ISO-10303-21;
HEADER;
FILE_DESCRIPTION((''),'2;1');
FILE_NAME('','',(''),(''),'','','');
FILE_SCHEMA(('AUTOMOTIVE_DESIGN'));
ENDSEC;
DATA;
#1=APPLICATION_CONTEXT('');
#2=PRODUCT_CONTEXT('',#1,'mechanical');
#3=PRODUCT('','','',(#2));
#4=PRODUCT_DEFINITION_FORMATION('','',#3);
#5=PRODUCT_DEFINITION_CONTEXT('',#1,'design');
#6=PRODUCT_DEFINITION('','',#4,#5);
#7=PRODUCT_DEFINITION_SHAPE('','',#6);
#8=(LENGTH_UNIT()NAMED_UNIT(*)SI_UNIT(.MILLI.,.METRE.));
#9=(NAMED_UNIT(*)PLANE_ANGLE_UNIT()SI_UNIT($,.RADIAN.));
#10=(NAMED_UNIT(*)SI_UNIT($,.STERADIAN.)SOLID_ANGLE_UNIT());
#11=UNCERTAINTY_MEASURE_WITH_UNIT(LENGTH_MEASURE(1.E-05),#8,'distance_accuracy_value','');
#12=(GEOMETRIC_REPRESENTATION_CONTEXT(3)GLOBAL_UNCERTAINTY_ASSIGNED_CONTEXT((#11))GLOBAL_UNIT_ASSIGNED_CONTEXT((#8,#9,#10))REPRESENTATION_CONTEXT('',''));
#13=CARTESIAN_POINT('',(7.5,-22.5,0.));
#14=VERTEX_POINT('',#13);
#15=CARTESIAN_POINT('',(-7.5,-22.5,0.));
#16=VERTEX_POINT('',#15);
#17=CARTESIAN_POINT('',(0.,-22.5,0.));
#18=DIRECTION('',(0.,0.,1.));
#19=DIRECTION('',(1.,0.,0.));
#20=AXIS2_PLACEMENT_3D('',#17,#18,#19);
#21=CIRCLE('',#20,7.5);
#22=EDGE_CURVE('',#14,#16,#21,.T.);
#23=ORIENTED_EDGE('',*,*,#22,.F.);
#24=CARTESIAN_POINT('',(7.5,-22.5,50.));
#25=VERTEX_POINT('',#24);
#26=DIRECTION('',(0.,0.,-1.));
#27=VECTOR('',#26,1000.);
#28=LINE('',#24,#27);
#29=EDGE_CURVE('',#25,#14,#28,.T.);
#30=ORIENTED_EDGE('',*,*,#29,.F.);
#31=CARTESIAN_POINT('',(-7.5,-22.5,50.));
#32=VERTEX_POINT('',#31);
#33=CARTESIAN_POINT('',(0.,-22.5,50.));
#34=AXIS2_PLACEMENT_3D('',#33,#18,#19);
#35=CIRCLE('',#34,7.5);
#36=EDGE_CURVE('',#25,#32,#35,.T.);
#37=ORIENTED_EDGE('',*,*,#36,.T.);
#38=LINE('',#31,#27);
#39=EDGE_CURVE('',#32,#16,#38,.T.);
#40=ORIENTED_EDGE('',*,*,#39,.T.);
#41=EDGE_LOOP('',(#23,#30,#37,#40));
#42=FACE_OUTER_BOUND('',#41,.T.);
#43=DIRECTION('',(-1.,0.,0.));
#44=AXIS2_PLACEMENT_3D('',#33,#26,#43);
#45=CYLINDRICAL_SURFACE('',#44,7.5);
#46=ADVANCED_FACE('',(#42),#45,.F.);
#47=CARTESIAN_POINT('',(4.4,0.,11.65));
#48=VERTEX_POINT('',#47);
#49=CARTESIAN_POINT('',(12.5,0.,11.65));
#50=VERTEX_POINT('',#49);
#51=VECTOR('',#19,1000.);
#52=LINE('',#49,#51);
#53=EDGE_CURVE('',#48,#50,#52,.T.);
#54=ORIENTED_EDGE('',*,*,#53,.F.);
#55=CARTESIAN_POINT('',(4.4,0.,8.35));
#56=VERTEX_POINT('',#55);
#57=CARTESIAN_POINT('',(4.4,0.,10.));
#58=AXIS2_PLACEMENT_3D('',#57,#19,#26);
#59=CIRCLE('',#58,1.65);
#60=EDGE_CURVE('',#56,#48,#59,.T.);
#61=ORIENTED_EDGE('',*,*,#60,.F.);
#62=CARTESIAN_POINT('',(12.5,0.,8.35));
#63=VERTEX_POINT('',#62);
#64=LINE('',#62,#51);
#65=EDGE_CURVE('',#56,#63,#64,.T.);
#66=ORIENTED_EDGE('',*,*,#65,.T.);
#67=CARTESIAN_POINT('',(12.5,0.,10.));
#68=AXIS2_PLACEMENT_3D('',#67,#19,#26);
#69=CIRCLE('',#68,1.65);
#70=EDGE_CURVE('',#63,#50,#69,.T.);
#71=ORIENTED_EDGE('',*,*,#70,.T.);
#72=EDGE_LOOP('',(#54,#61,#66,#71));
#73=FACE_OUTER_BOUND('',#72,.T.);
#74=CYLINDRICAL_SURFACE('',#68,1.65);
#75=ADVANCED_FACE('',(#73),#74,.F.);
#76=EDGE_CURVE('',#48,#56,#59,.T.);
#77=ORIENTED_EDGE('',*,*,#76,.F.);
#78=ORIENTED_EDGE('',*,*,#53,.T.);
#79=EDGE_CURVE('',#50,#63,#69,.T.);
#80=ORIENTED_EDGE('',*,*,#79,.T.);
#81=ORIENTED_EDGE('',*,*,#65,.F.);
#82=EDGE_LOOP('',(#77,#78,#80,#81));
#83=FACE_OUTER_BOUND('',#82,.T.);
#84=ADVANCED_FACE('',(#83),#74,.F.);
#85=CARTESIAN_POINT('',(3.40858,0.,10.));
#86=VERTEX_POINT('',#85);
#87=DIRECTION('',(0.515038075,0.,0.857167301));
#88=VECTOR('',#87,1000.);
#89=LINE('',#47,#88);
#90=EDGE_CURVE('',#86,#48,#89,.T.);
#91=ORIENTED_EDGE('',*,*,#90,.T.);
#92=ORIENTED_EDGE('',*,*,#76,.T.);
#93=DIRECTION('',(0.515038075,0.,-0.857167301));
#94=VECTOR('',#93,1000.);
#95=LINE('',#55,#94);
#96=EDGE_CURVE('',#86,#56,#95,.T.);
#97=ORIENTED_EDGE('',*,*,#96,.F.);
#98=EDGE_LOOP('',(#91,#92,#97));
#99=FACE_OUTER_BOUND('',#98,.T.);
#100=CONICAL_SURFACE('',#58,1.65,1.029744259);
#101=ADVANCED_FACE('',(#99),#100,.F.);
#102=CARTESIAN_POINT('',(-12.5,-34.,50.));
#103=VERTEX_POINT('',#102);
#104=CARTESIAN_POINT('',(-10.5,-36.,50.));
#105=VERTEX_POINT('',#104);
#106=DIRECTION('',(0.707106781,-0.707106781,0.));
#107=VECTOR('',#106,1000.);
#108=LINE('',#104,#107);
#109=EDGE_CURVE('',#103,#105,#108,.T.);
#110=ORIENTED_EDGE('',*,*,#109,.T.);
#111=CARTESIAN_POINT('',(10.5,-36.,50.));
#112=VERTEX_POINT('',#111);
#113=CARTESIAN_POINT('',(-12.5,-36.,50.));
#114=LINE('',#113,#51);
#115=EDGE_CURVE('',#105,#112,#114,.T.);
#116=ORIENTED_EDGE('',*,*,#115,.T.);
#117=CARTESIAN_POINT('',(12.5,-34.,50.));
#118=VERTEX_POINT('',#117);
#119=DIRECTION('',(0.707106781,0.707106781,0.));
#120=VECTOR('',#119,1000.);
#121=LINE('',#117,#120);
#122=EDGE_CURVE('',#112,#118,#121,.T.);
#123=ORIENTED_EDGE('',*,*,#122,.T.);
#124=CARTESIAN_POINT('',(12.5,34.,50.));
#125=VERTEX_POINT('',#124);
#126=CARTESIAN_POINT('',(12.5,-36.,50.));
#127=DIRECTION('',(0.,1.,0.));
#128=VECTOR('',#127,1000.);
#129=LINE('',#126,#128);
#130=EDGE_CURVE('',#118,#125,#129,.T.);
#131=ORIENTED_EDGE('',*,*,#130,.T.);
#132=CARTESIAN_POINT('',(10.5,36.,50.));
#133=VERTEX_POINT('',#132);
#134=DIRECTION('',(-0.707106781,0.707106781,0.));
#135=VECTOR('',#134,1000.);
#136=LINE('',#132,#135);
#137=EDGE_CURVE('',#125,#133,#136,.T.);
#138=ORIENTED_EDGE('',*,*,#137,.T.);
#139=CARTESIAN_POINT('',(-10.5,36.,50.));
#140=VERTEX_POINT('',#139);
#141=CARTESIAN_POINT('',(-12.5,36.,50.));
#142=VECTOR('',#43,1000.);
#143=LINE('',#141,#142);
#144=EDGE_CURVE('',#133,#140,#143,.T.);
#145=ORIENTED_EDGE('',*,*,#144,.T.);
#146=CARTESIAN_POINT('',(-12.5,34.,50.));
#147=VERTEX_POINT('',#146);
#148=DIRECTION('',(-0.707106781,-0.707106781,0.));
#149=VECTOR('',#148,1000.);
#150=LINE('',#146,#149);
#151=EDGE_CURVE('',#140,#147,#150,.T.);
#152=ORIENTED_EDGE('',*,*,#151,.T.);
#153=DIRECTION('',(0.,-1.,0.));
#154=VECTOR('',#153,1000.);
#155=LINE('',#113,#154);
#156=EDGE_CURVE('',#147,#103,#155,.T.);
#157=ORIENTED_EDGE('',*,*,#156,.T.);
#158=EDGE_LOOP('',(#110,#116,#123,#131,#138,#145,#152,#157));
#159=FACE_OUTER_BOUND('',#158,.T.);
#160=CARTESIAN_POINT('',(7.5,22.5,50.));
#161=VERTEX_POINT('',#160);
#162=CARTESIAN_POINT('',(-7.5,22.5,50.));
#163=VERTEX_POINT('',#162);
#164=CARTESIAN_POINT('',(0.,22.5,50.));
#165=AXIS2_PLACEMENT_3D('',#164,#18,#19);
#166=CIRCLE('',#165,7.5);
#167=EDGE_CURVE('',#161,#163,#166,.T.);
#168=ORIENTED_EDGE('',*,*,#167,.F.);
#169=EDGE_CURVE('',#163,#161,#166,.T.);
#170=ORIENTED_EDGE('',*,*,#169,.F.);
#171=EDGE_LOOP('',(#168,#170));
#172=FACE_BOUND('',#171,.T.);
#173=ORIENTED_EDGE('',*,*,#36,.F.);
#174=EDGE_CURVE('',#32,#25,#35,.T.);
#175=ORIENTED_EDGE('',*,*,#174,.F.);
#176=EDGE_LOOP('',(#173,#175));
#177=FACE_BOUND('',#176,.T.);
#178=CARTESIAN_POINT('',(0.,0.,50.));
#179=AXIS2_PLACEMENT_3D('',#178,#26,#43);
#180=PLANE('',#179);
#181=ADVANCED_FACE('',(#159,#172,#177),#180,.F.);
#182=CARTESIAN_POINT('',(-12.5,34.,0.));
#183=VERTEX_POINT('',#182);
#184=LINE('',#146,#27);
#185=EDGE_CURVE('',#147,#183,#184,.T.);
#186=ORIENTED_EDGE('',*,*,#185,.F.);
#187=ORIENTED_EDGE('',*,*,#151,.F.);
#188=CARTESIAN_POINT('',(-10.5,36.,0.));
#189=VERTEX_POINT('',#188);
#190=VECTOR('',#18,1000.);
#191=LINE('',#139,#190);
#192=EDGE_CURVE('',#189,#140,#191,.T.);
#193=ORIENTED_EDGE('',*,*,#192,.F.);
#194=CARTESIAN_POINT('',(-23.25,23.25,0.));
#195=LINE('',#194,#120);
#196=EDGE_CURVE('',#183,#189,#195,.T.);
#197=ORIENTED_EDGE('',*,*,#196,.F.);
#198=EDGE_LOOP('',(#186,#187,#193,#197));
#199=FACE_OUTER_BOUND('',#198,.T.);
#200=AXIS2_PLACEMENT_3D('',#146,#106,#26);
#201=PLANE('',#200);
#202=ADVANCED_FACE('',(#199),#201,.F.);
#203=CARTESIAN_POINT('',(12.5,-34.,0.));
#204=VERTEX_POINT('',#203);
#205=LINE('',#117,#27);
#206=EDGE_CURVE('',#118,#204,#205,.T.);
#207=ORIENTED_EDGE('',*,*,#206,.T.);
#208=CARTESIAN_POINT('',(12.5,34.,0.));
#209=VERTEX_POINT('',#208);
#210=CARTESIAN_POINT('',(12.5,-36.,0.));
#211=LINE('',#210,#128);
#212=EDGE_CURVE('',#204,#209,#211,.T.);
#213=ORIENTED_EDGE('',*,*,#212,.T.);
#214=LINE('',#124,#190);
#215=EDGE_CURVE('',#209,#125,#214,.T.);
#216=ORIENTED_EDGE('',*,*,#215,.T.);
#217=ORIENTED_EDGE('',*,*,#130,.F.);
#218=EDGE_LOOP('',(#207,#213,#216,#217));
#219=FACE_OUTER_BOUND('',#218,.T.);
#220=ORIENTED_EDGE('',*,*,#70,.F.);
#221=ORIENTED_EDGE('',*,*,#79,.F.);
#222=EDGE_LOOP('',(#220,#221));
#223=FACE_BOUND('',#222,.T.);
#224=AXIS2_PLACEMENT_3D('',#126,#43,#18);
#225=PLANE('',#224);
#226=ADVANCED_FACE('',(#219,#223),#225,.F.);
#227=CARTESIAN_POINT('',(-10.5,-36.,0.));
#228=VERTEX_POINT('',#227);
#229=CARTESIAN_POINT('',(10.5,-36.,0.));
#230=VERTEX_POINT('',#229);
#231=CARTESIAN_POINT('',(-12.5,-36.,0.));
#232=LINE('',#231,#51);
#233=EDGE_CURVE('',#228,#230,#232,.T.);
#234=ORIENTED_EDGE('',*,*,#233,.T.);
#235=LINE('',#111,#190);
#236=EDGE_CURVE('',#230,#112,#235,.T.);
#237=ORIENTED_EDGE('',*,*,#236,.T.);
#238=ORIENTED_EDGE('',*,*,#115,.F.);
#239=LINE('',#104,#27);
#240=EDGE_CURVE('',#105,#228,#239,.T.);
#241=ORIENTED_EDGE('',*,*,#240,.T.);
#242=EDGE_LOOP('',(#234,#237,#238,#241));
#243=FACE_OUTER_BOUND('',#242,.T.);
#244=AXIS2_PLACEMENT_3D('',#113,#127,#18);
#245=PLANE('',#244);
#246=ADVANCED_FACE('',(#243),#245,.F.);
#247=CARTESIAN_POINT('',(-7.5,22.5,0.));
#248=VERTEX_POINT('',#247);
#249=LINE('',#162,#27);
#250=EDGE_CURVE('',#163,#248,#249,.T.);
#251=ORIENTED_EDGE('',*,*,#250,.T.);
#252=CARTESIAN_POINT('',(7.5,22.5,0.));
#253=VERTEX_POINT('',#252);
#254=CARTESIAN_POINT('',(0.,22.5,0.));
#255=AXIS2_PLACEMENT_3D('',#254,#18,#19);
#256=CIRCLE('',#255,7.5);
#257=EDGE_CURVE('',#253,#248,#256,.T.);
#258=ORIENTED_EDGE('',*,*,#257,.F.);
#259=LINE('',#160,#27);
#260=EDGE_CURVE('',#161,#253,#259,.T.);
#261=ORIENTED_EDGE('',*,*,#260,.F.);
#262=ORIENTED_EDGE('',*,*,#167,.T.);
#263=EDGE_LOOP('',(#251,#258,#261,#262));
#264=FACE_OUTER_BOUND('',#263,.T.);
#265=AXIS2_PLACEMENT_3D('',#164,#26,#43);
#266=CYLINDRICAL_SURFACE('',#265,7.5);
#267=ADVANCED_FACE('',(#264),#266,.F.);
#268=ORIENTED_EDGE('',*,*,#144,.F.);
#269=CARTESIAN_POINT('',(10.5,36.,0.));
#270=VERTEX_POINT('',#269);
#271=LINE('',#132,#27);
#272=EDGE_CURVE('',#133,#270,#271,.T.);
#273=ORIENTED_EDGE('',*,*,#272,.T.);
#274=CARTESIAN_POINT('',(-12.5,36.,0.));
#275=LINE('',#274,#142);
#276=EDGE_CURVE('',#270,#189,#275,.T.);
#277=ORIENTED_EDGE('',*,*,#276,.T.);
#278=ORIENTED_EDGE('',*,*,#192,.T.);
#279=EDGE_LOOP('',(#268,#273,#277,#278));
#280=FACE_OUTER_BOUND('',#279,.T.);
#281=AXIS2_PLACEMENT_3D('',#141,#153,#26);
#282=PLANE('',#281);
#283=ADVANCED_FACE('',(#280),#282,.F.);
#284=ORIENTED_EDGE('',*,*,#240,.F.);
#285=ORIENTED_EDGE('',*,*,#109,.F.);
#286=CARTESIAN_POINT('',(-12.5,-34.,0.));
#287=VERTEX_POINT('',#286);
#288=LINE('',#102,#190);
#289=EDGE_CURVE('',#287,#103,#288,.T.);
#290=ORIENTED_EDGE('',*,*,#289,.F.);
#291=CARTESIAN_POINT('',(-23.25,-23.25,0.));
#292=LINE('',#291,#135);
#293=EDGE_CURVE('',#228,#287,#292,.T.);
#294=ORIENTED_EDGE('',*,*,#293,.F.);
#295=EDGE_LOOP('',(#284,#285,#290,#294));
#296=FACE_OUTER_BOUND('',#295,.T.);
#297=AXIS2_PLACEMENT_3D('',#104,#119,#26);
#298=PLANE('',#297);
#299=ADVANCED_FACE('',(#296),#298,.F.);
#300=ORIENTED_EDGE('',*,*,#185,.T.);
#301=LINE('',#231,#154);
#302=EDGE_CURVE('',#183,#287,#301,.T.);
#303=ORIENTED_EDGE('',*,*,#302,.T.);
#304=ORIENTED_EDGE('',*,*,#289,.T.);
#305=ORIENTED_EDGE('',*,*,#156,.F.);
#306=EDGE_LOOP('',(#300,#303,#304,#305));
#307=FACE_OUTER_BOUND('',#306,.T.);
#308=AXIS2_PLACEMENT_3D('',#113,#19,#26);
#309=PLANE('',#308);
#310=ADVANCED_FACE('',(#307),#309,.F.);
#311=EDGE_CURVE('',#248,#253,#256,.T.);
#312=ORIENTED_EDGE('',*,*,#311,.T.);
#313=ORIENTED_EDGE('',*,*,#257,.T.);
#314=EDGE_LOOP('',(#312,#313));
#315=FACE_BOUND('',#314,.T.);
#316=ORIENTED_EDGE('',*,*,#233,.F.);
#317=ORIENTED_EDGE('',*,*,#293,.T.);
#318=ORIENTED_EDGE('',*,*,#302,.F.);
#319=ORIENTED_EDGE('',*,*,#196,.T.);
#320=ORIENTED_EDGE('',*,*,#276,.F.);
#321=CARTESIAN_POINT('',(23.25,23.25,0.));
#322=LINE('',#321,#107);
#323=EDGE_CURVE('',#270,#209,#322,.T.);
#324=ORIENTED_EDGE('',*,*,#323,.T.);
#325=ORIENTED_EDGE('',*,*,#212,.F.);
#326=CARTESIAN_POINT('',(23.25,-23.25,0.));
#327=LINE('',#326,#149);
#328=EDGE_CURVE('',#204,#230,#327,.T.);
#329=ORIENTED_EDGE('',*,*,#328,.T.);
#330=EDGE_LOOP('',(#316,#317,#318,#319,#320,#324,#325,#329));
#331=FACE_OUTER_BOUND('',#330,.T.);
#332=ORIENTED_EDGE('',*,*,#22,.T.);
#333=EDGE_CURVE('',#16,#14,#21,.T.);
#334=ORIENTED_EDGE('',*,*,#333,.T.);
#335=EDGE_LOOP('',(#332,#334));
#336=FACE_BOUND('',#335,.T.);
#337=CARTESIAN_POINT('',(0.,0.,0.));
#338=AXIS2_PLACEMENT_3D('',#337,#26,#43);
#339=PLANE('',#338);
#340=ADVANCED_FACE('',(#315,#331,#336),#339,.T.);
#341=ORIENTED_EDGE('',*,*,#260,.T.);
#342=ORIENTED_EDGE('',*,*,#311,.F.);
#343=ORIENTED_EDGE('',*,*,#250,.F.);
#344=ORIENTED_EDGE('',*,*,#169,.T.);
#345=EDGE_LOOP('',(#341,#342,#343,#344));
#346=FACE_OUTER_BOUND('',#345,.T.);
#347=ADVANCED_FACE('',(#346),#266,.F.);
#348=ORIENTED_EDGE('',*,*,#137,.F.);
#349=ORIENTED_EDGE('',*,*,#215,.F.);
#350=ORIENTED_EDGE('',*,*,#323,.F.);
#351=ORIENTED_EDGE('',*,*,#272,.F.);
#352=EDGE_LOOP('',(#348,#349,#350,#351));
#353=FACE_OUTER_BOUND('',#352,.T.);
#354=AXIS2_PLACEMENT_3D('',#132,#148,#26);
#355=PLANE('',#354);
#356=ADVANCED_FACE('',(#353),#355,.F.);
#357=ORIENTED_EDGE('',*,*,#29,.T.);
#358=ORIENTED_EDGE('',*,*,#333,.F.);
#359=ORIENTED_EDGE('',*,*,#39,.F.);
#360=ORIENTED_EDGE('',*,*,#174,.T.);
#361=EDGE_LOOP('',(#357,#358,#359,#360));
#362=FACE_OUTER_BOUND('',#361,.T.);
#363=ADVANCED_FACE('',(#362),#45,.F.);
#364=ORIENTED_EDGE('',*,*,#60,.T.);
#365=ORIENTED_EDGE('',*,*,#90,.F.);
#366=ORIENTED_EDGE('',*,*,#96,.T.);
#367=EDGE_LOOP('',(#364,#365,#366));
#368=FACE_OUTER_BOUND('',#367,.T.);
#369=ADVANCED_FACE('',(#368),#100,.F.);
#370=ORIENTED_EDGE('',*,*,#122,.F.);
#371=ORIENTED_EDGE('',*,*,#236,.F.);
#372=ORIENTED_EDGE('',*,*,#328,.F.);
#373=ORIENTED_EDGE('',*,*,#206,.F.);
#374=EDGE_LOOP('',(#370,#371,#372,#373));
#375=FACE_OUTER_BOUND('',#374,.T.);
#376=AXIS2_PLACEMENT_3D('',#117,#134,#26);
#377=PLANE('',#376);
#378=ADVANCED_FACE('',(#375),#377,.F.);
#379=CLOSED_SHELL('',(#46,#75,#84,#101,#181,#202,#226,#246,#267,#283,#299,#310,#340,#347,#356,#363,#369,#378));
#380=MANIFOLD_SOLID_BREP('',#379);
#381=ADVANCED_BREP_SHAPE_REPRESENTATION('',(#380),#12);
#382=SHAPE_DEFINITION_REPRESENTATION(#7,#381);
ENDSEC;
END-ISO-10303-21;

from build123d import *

# Parameters (mm, degrees)
SKETCH_1_W             = 25
SKETCH_1_H             = 72
SKETCH_1_R             = 7.5
EXTRUDE_1_DEPTH        = 50
HOLE_WIZARD_M4_1_D     = 3.3
HOLE_WIZARD_M4_1_DEPTH = 8.1
HOLE_WIZARD_M4_1_TIP   = 0.991420021
CHAMFER_1_SIZE         = 2


with BuildPart() as part:
    # 草图1 → 凸台-拉伸1 (new body)
    with BuildSketch(Plane.XY):
        Rectangle(SKETCH_1_W, SKETCH_1_H)
        with Locations((0, 22.5)):
            Circle(SKETCH_1_R, mode=Mode.SUBTRACT)
        with Locations((0, -22.5)):
            Circle(SKETCH_1_R, mode=Mode.SUBTRACT)
    extrude(amount=EXTRUDE_1_DEPTH)

    # M4 螺纹孔1
    with Locations(Plane(origin=(12.5, 0, 10), x_dir=(0, 0, 1), z_dir=(1, 0, 0))):
        with Locations((0, 0)):
            Hole(HOLE_WIZARD_M4_1_D / 2, depth=HOLE_WIZARD_M4_1_DEPTH)
            with Locations((0, 0, -(HOLE_WIZARD_M4_1_DEPTH + HOLE_WIZARD_M4_1_TIP / 2))):  # 118° drill point
                Cone(0, HOLE_WIZARD_M4_1_D / 2, HOLE_WIZARD_M4_1_TIP, mode=Mode.SUBTRACT)

    # 倒角1
    chamfer_1_edges = [part.edges().sort_by_distance(p)[0] for p in [
        (12.5, -36, 25),
        (-12.5, -36, 25),
        (-12.5, 36, 25),
        (12.5, 36, 25),
    ]]
    chamfer(chamfer_1_edges, length=CHAMFER_1_SIZE)


solid = part.part
